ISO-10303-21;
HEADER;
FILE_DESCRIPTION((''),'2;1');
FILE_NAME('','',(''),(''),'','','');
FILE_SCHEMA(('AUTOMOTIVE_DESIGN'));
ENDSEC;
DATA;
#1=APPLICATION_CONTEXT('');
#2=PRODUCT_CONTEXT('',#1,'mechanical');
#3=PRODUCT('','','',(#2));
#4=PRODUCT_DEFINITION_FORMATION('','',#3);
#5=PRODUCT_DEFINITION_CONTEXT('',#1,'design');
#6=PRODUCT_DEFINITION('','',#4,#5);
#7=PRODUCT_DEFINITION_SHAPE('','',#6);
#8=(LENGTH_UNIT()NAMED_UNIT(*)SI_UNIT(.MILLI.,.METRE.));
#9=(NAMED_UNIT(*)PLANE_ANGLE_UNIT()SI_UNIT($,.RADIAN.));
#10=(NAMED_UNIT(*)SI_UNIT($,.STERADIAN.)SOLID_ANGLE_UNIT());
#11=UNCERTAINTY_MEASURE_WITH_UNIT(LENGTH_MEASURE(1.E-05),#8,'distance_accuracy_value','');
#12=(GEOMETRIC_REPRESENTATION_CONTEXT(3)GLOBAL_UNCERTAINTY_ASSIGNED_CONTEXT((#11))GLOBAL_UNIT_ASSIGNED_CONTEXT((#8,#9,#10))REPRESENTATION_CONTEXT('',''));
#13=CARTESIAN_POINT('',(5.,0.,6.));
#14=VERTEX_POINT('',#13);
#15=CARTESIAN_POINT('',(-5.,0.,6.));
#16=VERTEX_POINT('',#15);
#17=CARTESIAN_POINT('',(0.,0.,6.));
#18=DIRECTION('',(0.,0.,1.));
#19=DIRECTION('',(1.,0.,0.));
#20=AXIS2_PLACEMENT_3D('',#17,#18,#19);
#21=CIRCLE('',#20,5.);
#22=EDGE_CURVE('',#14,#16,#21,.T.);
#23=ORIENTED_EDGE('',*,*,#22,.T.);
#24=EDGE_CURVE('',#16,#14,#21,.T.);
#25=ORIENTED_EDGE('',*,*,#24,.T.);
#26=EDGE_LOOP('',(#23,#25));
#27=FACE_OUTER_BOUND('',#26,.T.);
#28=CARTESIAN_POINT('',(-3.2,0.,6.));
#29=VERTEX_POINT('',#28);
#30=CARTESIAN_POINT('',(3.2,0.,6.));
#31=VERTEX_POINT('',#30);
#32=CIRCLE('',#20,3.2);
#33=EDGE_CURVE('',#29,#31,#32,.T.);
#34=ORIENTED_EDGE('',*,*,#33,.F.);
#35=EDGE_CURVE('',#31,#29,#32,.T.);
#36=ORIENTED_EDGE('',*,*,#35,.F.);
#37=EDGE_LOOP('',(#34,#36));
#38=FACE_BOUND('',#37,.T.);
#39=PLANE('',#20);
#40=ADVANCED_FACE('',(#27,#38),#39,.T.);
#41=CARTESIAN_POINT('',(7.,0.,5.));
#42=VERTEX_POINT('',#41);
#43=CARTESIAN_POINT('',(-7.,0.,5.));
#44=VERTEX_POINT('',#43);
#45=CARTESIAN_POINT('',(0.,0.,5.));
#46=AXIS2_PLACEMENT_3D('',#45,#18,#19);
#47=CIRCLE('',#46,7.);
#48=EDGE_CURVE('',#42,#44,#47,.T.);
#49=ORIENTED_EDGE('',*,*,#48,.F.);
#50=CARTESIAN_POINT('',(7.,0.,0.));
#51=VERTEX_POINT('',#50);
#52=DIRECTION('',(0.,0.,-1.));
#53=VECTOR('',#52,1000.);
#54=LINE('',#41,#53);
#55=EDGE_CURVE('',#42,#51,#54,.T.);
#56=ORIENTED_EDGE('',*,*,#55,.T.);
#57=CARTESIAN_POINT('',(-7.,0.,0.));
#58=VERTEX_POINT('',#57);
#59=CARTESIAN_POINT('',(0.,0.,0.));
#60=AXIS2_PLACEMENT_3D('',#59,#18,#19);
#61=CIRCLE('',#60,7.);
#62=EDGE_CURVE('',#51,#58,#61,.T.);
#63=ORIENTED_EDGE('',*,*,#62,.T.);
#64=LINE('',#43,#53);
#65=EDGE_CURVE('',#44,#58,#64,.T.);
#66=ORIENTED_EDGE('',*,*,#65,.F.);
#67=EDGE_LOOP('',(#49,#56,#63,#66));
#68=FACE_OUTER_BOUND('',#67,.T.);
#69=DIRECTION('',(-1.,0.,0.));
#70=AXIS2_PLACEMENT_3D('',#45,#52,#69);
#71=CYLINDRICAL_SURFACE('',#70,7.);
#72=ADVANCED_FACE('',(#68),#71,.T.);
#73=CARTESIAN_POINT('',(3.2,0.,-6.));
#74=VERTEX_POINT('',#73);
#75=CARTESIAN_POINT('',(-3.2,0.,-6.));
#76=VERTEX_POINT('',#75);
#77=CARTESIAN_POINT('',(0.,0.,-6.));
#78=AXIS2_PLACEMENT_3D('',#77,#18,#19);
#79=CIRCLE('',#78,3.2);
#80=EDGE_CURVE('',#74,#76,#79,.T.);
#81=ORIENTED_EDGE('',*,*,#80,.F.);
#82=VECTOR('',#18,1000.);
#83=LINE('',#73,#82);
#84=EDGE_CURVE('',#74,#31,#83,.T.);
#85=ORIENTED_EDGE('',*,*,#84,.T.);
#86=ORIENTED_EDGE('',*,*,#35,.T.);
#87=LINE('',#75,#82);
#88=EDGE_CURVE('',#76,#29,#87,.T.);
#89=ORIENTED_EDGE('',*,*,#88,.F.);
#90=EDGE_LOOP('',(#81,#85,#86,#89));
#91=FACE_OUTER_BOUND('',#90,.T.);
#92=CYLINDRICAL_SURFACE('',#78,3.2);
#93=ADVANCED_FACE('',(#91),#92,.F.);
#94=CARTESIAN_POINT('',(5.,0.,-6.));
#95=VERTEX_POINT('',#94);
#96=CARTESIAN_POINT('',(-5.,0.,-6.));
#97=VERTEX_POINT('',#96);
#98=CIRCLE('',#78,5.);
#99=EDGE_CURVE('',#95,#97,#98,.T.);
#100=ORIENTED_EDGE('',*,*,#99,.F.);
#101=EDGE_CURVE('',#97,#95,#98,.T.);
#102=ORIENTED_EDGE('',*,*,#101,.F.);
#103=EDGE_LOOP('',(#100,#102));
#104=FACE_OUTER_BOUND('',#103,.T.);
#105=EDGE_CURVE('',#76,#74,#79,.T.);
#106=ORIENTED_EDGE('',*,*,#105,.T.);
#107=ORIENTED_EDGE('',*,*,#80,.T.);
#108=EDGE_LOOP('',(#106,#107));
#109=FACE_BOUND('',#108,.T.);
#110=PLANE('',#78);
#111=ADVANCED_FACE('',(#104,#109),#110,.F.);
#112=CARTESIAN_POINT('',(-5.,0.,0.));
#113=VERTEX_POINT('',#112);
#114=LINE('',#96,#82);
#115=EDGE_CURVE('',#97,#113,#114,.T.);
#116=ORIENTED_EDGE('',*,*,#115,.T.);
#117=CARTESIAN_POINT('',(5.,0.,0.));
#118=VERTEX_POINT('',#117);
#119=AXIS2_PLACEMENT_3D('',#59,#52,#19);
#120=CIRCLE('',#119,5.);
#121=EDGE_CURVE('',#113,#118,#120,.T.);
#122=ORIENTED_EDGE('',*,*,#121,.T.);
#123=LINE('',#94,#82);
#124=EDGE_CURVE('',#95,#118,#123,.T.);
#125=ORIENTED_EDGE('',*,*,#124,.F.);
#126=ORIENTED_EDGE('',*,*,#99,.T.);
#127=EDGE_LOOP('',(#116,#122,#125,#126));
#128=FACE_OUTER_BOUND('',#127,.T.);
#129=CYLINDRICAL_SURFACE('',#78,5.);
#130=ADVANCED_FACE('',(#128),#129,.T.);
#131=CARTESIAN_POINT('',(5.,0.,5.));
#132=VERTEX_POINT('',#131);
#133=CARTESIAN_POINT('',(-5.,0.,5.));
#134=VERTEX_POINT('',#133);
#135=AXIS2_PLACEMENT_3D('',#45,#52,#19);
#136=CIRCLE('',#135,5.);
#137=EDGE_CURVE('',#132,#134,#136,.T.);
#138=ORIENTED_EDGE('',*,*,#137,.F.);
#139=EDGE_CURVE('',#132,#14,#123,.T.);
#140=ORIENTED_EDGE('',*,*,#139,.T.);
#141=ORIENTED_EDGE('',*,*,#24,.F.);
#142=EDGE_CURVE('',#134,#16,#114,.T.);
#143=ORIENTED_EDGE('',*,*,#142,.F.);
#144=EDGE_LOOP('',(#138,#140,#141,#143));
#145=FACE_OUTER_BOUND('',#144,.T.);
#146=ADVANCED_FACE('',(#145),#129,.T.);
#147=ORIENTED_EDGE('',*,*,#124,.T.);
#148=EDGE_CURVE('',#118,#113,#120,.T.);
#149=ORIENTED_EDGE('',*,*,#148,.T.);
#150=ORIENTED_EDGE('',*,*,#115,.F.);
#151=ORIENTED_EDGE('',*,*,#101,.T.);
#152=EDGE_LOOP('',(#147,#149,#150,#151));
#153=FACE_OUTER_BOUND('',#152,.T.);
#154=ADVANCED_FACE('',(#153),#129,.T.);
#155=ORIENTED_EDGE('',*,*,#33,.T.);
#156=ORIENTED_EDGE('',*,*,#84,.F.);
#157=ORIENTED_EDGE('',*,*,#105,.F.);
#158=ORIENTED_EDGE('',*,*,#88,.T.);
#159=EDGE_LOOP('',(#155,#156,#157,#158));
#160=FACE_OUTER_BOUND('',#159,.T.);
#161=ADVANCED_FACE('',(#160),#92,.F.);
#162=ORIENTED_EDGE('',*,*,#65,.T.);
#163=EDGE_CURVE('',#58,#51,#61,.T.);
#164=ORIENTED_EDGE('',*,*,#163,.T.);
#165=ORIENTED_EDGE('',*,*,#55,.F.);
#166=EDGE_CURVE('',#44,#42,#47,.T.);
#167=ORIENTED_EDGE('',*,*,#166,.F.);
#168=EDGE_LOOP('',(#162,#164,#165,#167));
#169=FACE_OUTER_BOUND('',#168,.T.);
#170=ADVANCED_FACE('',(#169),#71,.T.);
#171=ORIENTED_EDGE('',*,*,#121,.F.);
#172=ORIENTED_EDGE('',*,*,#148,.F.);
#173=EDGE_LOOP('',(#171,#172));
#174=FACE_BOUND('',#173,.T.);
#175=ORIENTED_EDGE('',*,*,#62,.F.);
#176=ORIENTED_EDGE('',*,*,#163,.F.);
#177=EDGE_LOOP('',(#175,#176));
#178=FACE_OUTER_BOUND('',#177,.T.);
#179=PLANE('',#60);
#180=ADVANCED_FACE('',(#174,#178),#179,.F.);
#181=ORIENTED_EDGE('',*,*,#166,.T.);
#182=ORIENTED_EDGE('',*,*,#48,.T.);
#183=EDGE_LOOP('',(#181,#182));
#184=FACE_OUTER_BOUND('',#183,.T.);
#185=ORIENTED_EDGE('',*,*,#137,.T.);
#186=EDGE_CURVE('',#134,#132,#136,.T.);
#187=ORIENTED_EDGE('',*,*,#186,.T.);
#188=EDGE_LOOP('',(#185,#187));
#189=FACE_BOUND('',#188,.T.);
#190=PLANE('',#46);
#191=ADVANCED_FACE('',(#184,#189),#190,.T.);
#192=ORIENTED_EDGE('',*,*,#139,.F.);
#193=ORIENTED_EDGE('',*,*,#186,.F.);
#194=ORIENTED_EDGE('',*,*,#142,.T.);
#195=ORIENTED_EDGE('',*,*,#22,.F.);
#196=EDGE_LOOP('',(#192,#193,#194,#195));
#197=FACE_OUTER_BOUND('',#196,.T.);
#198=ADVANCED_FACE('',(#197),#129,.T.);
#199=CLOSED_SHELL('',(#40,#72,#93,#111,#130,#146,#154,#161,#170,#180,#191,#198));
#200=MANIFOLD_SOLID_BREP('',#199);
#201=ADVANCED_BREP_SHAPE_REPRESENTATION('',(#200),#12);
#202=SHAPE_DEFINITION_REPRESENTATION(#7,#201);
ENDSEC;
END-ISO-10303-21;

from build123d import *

# Parameters (mm, degrees)
SKETCH_1_R      = 5
SKETCH_1_R_2    = 3.2
EXTRUDE_1_DEPTH = 6
SKETCH_2_R      = 7
SKETCH_2_R_2    = 3.2
EXTRUDE_2_DEPTH = 5


with BuildPart() as part:
    # 草图1 → 凸台-拉伸1 (new, symmetric)
    with BuildSketch(Plane.XY):
        Circle(SKETCH_1_R)
        Circle(SKETCH_1_R_2, mode=Mode.SUBTRACT)
    extrude(amount=EXTRUDE_1_DEPTH, both=True)

    # 草图2 → 凸台-拉伸2 (add)
    with BuildSketch(Plane.XY):
        Circle(SKETCH_2_R)
        Circle(SKETCH_2_R_2, mode=Mode.SUBTRACT)
    extrude(amount=EXTRUDE_2_DEPTH)


solid = part.part
